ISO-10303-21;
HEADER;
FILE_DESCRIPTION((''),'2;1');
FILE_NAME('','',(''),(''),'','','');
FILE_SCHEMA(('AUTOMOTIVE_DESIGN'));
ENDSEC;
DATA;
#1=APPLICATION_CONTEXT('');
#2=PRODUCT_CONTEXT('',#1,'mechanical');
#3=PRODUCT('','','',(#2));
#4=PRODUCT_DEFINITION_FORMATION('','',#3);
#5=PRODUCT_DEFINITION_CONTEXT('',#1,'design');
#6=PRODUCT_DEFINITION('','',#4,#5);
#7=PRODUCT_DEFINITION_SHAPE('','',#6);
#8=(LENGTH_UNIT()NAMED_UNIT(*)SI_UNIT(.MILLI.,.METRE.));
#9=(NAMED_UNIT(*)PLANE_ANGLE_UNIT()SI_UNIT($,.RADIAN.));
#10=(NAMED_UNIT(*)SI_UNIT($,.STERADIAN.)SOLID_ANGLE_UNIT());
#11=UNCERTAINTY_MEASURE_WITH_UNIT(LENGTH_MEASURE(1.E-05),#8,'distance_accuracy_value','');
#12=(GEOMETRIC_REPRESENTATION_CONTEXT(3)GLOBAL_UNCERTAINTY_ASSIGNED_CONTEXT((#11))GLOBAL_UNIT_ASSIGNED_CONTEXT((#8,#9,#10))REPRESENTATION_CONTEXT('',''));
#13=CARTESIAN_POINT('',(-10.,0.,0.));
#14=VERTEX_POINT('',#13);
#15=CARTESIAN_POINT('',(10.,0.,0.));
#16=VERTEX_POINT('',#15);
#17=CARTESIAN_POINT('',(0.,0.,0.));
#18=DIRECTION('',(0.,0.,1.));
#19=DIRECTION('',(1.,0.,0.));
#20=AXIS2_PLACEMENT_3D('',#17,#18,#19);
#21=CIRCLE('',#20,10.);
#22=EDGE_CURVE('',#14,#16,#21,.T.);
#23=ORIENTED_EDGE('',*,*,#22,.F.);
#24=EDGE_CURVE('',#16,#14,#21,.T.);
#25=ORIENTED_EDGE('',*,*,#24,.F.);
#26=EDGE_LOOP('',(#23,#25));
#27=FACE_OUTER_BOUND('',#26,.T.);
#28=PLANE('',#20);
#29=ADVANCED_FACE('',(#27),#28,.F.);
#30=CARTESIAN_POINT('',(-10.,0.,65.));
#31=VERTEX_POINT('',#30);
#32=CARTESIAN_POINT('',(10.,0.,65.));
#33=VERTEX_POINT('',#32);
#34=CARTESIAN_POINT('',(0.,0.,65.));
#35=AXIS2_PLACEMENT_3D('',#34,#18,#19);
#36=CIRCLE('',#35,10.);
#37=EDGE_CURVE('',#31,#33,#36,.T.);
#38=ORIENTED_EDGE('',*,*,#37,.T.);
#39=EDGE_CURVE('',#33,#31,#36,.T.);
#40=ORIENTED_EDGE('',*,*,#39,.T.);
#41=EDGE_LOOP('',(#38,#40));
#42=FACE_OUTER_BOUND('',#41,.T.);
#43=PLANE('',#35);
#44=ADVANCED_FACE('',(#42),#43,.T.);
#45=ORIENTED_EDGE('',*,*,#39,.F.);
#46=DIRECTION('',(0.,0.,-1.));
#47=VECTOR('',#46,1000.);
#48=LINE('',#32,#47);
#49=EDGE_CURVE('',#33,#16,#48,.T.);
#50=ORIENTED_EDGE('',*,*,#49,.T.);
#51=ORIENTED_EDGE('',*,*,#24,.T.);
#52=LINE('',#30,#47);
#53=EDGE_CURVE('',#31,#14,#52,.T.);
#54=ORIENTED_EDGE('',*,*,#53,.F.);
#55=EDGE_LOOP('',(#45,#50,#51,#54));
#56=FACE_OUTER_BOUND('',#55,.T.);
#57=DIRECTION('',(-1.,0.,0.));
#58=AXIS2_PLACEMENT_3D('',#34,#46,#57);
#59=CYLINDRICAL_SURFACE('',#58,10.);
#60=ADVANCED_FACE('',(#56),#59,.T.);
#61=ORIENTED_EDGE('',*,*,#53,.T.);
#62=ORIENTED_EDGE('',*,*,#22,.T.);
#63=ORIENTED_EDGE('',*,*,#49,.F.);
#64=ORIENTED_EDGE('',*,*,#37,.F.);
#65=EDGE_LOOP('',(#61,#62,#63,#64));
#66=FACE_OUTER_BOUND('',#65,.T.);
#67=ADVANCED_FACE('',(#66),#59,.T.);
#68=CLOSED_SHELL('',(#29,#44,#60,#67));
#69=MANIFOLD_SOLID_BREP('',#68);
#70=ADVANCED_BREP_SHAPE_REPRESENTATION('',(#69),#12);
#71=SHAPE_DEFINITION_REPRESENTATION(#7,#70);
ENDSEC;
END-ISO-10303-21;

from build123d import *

# Parameters (mm, degrees)
SKETCH_1_R      = 10
EXTRUDE_1_DEPTH = 65


with BuildPart() as part:
    # 草图1 → 凸台-拉伸1 (new body)
    with BuildSketch(Plane.XY):
        Circle(SKETCH_1_R)
    extrude(amount=EXTRUDE_1_DEPTH)


solid = part.part
